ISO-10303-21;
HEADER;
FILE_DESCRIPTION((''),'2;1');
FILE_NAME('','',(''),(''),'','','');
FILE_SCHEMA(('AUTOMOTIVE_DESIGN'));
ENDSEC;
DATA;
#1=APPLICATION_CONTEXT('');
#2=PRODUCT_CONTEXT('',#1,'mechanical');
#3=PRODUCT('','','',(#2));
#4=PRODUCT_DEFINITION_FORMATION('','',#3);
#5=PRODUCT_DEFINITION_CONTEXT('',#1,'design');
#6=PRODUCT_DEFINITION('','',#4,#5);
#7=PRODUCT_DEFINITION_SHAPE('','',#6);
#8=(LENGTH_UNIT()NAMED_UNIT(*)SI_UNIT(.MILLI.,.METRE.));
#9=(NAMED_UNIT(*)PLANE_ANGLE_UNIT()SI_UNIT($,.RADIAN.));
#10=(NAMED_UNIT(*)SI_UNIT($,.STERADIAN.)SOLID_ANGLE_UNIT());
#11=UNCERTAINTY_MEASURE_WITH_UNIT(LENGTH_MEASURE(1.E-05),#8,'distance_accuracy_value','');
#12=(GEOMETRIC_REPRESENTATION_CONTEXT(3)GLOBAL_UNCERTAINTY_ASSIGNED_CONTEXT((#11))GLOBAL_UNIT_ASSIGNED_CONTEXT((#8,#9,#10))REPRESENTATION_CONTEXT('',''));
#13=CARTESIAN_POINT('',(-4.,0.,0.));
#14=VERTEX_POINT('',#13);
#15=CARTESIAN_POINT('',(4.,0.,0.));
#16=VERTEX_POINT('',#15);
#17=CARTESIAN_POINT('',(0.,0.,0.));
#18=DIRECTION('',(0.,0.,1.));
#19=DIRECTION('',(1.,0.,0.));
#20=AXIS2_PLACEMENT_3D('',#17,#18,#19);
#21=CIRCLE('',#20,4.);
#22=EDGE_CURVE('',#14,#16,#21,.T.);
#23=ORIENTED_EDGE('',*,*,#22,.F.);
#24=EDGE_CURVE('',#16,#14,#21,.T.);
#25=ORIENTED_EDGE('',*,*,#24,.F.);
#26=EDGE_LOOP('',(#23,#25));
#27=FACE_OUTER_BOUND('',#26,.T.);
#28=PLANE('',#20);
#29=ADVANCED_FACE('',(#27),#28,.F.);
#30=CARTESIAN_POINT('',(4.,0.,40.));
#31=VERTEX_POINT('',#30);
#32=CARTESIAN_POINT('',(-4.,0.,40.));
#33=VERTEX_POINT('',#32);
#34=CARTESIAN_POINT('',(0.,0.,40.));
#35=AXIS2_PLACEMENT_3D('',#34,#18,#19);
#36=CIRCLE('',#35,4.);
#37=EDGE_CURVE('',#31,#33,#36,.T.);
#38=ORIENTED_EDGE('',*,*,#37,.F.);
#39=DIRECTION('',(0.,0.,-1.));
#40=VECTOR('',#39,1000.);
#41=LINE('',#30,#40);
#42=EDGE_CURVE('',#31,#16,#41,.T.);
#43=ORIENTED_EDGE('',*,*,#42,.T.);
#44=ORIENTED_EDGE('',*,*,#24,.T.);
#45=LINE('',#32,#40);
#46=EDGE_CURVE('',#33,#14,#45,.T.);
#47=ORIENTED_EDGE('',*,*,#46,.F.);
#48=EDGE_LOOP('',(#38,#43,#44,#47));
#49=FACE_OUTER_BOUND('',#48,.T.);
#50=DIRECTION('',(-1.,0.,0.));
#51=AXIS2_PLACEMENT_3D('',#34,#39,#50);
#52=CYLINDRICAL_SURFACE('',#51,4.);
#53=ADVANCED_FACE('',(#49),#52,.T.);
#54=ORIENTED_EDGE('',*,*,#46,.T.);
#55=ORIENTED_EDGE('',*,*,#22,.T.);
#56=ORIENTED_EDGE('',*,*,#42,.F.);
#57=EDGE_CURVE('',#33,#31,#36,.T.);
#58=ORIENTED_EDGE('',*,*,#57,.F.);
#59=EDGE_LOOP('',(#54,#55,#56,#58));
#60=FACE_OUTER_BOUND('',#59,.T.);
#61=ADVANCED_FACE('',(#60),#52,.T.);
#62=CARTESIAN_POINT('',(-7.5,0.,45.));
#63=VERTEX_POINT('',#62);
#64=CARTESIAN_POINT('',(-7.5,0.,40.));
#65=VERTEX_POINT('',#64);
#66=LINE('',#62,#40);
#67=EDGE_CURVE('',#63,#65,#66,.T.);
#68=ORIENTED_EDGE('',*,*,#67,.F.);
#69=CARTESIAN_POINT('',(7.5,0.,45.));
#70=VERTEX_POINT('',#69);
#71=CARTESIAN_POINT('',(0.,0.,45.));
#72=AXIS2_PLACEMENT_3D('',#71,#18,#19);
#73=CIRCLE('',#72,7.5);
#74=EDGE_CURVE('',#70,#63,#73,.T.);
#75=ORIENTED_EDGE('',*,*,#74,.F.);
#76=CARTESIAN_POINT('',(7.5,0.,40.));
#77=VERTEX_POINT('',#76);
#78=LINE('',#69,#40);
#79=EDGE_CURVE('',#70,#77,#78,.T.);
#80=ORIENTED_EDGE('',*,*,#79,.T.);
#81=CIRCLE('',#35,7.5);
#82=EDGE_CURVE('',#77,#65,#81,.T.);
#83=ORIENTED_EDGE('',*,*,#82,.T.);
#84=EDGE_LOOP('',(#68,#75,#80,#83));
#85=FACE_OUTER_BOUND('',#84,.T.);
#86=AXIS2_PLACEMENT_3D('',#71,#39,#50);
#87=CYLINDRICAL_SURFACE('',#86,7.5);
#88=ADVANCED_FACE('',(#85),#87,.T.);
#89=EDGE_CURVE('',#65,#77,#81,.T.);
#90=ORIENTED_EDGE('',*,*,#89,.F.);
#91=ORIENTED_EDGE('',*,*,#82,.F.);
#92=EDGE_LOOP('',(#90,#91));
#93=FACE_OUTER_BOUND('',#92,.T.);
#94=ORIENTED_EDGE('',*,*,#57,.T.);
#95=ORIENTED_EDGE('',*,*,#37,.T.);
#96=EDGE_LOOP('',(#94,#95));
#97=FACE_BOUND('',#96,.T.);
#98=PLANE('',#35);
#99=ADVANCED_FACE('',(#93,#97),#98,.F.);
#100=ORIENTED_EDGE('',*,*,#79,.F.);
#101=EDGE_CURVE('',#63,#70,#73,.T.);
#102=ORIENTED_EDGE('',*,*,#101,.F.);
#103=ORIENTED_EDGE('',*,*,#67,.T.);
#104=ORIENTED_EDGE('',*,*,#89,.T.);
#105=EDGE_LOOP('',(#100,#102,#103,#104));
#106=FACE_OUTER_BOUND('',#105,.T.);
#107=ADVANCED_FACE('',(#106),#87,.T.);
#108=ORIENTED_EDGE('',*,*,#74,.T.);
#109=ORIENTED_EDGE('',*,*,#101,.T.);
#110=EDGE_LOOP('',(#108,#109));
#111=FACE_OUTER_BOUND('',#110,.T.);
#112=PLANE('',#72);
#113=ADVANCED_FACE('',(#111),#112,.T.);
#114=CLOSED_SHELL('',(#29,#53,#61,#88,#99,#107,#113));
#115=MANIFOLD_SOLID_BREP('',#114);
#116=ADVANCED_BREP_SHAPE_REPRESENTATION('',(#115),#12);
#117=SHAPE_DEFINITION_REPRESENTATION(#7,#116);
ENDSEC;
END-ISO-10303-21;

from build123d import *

# Parameters (mm, degrees)
SKETCH1_R           = 4
BOSS_EXTRUDE1_DEPTH = 40
SKETCH2_R           = 7.5
BOSS_EXTRUDE2_DEPTH = 5


with BuildPart() as part:
    # Sketch1 → Boss-Extrude1 (new body)
    with BuildSketch(Plane.XY):
        Circle(SKETCH1_R)
    extrude(amount=BOSS_EXTRUDE1_DEPTH)

    # Sketch2 → Boss-Extrude2 (add)
    with BuildSketch(Plane.XY.offset(40)):
        Circle(SKETCH2_R)
    extrude(amount=BOSS_EXTRUDE2_DEPTH)


solid = part.part
